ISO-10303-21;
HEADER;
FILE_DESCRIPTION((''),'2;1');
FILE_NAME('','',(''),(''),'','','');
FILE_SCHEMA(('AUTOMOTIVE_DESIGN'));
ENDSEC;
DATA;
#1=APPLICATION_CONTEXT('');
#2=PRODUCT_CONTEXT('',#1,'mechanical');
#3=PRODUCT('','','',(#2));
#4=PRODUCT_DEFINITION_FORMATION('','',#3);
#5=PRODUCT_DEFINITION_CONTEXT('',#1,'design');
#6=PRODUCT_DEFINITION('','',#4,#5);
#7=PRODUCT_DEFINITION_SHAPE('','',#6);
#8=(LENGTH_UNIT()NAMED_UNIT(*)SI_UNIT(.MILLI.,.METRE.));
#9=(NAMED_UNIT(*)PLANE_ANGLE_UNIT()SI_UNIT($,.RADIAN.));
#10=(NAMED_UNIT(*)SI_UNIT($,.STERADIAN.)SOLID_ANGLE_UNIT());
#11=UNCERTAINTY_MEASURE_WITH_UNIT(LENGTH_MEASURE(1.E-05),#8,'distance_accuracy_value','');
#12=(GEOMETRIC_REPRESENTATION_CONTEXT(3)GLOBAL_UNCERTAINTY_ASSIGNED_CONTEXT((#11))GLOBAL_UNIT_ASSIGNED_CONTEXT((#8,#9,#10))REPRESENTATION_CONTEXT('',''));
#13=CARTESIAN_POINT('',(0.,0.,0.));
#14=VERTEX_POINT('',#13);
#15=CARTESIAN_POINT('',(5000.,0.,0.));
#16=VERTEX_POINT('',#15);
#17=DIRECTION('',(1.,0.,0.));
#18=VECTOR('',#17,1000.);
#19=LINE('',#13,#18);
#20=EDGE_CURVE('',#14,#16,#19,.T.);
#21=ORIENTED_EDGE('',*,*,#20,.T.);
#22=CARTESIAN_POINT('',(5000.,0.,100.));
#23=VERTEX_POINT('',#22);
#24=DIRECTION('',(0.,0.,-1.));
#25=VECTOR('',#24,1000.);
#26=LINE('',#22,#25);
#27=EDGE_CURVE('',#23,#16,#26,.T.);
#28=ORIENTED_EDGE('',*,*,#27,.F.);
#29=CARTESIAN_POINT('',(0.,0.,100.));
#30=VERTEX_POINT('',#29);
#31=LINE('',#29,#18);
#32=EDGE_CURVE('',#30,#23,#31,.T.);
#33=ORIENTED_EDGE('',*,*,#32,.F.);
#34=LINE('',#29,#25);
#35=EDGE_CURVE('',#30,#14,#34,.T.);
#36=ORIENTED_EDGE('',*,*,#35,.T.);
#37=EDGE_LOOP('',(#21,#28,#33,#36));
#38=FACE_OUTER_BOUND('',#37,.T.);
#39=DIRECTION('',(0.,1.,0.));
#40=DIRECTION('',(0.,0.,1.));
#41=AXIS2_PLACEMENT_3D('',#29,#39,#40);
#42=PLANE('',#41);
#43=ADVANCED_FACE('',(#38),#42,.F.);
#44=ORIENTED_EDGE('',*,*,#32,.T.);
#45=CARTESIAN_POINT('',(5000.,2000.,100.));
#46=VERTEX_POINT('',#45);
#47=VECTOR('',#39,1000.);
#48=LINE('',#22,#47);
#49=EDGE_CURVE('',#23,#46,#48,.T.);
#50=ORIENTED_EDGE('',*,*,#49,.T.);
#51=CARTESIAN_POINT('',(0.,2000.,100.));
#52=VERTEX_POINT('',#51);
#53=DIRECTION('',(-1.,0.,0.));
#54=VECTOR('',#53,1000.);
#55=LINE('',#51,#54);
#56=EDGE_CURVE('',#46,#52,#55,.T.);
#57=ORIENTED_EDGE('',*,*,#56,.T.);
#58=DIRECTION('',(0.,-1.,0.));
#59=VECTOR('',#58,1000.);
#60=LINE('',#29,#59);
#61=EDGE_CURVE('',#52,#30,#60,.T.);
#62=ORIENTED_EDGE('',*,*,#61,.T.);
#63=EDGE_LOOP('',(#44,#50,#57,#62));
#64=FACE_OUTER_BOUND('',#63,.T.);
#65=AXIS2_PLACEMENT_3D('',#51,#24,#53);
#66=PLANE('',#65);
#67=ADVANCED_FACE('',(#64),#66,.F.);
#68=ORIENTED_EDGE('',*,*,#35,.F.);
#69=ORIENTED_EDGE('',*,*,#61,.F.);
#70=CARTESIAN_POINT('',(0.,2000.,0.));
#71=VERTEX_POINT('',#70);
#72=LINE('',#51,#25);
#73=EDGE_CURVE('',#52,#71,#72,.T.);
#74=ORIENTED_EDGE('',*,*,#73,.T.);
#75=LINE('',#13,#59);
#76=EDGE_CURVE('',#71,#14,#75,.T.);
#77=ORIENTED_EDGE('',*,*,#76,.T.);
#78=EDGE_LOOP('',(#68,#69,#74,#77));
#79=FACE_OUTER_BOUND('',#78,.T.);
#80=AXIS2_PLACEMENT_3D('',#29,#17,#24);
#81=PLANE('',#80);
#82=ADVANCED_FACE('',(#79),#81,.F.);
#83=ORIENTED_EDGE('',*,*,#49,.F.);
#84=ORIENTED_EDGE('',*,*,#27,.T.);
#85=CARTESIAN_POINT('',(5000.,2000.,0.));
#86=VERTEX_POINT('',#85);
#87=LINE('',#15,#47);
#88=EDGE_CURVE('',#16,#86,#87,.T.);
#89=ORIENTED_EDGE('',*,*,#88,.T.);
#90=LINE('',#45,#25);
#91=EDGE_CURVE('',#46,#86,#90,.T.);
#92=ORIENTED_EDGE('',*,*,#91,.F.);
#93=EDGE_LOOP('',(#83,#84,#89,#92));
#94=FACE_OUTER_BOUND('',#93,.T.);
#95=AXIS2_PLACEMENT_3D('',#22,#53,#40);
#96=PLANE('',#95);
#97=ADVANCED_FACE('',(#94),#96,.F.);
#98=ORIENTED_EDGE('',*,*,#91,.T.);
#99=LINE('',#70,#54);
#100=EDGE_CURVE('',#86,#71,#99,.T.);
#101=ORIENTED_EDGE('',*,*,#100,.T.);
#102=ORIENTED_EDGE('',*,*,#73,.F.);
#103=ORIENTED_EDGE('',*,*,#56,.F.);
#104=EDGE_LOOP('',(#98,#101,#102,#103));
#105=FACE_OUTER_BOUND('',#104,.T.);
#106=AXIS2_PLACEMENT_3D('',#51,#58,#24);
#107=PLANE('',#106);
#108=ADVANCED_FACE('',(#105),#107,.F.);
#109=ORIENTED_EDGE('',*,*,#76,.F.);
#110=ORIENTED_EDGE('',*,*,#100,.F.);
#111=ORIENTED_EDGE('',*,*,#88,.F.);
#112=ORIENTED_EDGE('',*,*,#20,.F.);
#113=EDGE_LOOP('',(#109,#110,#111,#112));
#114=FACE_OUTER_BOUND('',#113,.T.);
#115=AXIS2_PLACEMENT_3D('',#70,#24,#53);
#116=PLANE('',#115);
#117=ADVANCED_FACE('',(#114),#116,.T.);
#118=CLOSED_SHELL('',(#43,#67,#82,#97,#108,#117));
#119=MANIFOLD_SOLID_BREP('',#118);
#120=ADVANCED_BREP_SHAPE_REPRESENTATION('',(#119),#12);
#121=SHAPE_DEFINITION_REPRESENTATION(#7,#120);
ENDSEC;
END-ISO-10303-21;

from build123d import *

# Parameters (mm, degrees)
SKETCH1_W           = 5000
SKETCH1_H           = 2000
BOSS_EXTRUDE1_DEPTH = 100


with BuildPart() as part:
    # Sketch1 → Boss-Extrude1 (new body)
    with BuildSketch(Plane.XY):
        with Locations((2500, 1000)):
            Rectangle(SKETCH1_W, SKETCH1_H)
    extrude(amount=BOSS_EXTRUDE1_DEPTH)


solid = part.part
